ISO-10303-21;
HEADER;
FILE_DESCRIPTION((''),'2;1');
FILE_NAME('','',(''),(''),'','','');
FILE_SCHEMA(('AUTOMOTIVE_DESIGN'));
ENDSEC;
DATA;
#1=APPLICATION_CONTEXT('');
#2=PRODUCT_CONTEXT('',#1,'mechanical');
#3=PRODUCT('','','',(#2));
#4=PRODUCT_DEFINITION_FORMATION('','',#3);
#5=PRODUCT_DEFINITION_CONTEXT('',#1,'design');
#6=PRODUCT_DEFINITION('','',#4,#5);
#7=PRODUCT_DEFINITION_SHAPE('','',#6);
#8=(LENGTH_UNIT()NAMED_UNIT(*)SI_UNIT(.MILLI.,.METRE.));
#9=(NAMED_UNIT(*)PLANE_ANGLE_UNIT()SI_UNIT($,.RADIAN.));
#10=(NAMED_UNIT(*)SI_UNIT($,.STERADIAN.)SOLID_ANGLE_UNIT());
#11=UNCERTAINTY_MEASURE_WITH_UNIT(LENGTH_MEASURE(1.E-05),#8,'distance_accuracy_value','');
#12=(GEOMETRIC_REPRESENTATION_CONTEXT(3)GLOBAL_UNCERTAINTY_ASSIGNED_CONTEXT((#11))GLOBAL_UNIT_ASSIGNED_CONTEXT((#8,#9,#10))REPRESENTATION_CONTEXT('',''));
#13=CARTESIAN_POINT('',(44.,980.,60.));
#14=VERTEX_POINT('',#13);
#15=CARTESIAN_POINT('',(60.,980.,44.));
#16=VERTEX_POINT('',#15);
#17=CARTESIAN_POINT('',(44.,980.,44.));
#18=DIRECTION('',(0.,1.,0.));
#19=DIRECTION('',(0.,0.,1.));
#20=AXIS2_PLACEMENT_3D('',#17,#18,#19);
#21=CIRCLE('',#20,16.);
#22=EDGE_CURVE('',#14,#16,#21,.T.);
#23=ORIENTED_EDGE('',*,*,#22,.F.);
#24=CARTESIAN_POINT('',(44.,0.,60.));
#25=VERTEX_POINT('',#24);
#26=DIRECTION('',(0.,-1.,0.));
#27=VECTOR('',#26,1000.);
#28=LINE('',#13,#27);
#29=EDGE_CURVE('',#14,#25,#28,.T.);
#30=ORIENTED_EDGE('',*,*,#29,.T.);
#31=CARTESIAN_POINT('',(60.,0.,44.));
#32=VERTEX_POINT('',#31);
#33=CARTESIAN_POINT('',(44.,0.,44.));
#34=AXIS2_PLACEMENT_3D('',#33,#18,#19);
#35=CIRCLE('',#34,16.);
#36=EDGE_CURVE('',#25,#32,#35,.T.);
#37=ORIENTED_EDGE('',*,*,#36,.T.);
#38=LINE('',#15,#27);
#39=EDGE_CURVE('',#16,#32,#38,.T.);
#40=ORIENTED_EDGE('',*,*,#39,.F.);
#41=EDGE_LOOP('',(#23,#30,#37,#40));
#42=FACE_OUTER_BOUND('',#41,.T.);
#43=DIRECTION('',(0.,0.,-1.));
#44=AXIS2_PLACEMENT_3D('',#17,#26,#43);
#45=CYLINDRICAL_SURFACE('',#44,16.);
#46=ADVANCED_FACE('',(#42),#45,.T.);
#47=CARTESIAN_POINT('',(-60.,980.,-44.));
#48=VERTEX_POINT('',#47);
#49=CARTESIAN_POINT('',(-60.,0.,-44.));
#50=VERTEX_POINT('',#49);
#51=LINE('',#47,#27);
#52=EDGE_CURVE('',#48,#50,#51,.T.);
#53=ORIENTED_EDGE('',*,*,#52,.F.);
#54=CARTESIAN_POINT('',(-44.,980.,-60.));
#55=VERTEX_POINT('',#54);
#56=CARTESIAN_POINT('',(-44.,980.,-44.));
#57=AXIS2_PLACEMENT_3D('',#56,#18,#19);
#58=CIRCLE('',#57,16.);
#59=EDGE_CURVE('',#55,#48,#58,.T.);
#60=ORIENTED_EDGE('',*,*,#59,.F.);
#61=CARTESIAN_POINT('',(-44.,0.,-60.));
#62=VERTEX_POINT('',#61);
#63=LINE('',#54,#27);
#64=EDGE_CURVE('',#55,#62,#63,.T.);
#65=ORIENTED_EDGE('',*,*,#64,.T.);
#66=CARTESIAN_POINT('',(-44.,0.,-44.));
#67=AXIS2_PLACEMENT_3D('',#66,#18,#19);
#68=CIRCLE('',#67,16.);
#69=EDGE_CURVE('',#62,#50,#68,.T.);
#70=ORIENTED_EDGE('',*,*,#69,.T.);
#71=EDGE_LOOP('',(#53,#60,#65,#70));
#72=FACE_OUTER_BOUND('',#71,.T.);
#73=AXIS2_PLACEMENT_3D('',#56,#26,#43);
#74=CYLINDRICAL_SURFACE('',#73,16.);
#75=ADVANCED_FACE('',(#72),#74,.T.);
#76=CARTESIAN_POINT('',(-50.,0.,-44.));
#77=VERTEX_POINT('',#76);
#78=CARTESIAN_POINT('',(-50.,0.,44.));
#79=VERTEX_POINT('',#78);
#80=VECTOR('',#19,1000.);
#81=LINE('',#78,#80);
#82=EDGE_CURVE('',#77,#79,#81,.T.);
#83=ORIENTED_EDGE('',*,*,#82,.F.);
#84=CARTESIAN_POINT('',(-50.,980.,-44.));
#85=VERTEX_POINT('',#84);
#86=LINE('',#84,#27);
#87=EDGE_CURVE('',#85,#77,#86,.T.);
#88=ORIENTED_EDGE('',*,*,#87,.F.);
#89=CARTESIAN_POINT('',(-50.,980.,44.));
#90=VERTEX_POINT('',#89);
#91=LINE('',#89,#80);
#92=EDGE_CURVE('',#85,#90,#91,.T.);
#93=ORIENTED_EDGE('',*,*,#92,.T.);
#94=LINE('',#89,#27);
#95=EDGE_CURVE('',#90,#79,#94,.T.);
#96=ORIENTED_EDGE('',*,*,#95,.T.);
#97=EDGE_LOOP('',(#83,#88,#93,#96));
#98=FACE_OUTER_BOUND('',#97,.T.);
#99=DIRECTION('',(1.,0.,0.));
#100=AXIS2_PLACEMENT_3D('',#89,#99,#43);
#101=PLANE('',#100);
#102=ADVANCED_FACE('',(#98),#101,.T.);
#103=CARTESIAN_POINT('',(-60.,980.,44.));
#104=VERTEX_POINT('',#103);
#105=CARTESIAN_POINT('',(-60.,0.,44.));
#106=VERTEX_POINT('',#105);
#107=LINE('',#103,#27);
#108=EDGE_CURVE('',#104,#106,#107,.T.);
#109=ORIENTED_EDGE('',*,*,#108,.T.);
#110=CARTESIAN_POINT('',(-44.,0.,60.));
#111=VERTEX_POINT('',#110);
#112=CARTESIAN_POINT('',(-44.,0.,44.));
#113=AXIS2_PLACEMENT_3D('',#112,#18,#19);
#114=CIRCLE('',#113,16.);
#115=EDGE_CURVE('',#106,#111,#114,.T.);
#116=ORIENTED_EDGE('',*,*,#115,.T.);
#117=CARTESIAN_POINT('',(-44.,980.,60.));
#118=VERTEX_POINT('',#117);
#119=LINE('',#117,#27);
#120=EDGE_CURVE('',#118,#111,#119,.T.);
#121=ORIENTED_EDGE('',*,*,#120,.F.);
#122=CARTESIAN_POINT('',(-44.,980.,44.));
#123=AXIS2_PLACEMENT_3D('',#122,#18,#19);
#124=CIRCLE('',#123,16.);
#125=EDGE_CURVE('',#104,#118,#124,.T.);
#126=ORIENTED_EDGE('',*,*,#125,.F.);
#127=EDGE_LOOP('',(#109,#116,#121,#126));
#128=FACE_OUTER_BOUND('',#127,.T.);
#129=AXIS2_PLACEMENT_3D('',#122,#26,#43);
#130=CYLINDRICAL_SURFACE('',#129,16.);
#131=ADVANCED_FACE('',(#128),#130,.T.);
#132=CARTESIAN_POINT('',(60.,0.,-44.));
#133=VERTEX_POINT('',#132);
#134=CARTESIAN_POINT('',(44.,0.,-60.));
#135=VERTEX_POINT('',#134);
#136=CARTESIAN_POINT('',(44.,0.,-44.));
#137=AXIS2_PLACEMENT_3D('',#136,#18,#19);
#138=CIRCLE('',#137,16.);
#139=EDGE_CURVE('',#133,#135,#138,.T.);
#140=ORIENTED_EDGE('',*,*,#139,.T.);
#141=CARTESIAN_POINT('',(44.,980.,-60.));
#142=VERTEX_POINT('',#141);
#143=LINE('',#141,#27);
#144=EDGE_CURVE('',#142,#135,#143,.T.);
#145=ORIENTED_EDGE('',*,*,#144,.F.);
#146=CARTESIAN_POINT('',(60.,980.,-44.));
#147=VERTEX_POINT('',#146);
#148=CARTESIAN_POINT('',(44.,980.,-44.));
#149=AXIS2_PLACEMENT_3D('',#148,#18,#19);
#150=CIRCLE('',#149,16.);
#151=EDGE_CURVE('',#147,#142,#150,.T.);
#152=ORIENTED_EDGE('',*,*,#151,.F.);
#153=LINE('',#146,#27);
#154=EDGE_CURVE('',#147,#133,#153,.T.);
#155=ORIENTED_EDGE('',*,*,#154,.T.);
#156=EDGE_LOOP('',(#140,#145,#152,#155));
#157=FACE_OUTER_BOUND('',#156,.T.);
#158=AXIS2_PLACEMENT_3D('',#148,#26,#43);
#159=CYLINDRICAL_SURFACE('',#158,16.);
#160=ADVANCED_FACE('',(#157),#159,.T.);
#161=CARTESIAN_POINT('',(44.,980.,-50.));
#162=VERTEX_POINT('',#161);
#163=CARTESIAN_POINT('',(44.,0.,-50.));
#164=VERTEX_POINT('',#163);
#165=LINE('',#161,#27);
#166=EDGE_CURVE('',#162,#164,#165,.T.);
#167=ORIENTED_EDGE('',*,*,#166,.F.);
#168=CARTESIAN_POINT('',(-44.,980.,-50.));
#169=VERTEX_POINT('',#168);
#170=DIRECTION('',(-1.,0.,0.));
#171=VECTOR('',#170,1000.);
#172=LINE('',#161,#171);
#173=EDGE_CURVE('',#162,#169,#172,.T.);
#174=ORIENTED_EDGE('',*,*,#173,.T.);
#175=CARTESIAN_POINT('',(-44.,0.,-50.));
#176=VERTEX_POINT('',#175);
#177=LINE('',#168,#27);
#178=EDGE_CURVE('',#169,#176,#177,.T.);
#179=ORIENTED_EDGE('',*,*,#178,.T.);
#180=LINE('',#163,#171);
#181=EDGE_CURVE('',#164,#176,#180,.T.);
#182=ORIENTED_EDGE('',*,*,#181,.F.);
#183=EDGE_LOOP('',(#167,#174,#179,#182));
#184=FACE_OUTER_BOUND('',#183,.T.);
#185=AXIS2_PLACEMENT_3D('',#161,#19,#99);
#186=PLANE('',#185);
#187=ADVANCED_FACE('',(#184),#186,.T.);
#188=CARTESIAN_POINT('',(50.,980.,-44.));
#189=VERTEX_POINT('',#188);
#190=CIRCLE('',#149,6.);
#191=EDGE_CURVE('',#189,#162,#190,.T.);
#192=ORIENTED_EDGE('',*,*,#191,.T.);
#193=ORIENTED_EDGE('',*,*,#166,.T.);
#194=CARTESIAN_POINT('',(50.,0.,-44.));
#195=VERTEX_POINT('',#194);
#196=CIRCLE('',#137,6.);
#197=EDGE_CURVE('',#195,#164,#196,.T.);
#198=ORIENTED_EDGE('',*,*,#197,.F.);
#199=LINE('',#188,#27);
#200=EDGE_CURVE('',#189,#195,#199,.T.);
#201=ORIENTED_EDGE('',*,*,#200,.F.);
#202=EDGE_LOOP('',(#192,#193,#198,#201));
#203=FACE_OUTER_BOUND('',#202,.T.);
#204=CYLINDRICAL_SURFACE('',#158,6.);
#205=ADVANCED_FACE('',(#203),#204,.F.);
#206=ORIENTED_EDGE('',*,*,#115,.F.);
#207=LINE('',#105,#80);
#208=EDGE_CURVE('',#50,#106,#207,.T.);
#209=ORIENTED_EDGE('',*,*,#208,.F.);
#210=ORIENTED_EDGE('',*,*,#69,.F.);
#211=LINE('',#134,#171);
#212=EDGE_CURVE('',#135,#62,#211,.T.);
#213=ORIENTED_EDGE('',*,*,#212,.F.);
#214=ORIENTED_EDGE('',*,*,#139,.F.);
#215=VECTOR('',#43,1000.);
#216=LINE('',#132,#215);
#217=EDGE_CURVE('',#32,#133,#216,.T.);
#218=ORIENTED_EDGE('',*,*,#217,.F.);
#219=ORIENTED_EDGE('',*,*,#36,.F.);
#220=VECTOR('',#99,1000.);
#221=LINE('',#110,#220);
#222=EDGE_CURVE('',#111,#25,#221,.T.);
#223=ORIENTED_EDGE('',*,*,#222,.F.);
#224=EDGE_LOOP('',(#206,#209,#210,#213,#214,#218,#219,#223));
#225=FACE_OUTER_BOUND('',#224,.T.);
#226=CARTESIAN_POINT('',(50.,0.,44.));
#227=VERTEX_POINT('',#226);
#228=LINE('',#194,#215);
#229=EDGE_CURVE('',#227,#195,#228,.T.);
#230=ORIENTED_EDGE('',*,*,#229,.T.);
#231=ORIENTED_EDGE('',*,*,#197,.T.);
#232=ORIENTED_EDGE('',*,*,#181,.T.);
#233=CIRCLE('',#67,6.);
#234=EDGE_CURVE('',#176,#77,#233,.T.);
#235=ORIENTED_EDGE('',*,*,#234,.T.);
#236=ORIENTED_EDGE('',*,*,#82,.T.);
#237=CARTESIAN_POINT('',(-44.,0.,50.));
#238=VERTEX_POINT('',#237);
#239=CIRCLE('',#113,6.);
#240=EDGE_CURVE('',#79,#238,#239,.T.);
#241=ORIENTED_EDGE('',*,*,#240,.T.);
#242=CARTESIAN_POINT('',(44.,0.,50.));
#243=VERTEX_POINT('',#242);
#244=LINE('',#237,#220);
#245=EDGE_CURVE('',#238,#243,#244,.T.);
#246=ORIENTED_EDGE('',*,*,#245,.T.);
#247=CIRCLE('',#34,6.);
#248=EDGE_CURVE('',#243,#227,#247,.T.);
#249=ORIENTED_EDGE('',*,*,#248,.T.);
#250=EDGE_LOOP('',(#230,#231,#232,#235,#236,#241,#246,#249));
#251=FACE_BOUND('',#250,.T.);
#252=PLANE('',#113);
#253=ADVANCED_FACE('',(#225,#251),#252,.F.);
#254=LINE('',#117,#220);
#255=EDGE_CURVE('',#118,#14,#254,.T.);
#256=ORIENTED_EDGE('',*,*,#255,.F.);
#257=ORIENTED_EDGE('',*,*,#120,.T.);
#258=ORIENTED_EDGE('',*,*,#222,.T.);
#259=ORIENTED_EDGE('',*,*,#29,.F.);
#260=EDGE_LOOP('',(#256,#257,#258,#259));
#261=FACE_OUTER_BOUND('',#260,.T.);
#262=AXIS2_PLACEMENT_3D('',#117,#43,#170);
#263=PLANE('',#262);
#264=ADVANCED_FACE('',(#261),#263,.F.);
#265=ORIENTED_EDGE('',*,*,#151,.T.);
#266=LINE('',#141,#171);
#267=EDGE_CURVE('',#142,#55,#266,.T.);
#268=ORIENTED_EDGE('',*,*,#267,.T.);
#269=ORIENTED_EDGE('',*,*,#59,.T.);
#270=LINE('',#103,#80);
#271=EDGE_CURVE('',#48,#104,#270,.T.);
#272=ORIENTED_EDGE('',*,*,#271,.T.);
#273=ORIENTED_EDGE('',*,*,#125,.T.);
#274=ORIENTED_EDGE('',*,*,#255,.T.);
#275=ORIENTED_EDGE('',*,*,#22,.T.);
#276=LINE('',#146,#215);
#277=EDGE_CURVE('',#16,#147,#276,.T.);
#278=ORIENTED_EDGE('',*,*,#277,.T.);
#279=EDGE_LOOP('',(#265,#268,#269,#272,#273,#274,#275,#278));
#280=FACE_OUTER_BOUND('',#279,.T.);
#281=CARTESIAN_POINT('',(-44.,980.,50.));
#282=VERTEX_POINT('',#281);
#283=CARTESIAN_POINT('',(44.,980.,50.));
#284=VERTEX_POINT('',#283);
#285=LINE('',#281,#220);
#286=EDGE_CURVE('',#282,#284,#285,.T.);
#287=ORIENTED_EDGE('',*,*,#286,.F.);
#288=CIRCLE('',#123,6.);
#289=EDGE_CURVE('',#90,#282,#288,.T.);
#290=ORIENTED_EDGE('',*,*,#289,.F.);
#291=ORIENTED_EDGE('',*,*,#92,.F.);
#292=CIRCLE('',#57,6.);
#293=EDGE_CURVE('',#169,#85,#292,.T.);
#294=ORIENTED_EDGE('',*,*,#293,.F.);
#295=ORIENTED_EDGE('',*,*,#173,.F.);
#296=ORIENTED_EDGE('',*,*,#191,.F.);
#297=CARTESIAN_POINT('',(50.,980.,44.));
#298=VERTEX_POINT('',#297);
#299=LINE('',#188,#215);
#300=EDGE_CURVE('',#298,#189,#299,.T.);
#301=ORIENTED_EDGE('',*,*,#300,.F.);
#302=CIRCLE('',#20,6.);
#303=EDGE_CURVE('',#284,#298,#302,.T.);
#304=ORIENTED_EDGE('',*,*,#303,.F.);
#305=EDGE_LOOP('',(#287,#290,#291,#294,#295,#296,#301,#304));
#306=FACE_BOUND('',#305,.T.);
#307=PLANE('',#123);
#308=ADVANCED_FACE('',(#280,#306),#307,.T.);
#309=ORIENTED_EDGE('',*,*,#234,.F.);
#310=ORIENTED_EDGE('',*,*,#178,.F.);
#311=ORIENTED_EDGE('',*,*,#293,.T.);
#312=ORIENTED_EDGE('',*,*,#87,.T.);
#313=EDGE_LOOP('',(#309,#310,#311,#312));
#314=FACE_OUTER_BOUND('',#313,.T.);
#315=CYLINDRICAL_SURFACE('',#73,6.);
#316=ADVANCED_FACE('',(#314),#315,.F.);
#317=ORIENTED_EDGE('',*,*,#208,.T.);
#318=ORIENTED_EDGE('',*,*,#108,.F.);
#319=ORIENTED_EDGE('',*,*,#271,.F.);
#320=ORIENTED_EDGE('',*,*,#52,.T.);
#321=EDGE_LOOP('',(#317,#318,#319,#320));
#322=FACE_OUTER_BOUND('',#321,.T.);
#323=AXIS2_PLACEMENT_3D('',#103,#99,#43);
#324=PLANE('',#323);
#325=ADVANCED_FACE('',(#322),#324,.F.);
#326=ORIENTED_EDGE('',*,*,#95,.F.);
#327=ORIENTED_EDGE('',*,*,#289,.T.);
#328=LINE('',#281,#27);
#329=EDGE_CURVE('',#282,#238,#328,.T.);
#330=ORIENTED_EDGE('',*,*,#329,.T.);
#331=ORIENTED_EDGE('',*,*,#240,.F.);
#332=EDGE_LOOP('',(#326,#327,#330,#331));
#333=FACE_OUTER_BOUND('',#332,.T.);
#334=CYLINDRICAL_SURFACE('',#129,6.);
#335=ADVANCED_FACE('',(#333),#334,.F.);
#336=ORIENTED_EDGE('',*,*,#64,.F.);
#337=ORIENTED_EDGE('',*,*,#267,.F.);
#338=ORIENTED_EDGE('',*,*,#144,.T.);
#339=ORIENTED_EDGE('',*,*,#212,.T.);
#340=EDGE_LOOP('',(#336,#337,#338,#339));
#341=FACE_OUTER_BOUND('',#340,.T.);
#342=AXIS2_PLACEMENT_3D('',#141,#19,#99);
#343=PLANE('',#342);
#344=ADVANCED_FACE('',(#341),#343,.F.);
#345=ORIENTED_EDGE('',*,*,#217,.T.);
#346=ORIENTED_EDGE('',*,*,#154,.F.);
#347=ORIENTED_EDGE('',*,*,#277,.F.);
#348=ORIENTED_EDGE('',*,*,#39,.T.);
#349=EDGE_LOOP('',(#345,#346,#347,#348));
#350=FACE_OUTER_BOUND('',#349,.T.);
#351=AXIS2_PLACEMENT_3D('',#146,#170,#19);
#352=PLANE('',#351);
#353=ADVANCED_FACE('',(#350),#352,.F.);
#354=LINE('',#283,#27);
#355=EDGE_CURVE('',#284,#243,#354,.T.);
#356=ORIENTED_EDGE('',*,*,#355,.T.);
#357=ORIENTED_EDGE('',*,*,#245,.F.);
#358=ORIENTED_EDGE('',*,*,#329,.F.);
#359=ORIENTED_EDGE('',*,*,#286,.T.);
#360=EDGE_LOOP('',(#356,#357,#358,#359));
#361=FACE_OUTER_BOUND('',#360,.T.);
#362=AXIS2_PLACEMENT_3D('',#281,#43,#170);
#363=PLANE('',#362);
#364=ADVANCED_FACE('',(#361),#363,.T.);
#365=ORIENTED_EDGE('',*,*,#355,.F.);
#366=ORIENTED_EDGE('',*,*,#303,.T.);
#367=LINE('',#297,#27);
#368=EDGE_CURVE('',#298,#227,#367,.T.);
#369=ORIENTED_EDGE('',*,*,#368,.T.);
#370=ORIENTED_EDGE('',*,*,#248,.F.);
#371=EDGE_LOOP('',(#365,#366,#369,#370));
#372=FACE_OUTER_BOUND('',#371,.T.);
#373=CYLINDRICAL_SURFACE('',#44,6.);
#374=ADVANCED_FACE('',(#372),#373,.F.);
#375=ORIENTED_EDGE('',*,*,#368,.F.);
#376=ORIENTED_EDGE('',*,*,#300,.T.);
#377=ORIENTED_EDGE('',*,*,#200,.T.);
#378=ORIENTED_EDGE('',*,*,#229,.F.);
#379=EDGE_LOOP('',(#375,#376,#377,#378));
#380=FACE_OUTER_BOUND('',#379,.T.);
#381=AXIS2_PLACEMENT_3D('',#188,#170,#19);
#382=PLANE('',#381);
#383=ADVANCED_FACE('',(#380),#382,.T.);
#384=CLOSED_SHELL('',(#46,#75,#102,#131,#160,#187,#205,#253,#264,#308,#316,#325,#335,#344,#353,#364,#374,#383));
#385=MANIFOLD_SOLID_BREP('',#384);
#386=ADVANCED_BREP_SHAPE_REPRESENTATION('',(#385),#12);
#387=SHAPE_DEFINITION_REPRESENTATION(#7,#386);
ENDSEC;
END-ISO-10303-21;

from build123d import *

# Parameters (mm, degrees)
GB_T6728_2002_120_120_10_1_DEPTH = 980


with BuildPart() as part:
    # Sketch12 → 结构用冷弯空心方钢(gb t6728-2002) 120×120×10(1) (new body)
    with BuildSketch(Plane(origin=(0, 0, 0), x_dir=(-1, 0, 0), z_dir=(0, 1, 0))):
        with BuildLine():
            Line((-44, -60), (44, -60))
            ThreePointArc((44, -60), (55.313708499, -55.313708499), (60, -44))
            Line((60, -44), (60, 44))
            ThreePointArc((60, 44), (55.313708499, 55.313708499), (44, 60))
            Line((44, 60), (-44, 60))
            ThreePointArc((-44, 60), (-55.313708499, 55.313708499), (-60, 44))
            Line((-60, 44), (-60, -44))
            ThreePointArc((-60, -44), (-55.313708499, -55.313708499), (-44, -60))
        make_face()
        with BuildLine():
            Line((-44, -50), (44, -50))
            ThreePointArc((44, -50), (48.242640687, -48.242640687), (50, -44))
            Line((50, -44), (50, 44))
            ThreePointArc((50, 44), (48.242640687, 48.242640687), (44, 50))
            Line((44, 50), (-44, 50))
            ThreePointArc((-44, 50), (-48.242640687, 48.242640687), (-50, 44))
            Line((-50, 44), (-50, -44))
            ThreePointArc((-50, -44), (-48.242640687, -48.242640687), (-44, -50))
        make_face(mode=Mode.SUBTRACT)
    extrude(amount=GB_T6728_2002_120_120_10_1_DEPTH)


solid = part.part
